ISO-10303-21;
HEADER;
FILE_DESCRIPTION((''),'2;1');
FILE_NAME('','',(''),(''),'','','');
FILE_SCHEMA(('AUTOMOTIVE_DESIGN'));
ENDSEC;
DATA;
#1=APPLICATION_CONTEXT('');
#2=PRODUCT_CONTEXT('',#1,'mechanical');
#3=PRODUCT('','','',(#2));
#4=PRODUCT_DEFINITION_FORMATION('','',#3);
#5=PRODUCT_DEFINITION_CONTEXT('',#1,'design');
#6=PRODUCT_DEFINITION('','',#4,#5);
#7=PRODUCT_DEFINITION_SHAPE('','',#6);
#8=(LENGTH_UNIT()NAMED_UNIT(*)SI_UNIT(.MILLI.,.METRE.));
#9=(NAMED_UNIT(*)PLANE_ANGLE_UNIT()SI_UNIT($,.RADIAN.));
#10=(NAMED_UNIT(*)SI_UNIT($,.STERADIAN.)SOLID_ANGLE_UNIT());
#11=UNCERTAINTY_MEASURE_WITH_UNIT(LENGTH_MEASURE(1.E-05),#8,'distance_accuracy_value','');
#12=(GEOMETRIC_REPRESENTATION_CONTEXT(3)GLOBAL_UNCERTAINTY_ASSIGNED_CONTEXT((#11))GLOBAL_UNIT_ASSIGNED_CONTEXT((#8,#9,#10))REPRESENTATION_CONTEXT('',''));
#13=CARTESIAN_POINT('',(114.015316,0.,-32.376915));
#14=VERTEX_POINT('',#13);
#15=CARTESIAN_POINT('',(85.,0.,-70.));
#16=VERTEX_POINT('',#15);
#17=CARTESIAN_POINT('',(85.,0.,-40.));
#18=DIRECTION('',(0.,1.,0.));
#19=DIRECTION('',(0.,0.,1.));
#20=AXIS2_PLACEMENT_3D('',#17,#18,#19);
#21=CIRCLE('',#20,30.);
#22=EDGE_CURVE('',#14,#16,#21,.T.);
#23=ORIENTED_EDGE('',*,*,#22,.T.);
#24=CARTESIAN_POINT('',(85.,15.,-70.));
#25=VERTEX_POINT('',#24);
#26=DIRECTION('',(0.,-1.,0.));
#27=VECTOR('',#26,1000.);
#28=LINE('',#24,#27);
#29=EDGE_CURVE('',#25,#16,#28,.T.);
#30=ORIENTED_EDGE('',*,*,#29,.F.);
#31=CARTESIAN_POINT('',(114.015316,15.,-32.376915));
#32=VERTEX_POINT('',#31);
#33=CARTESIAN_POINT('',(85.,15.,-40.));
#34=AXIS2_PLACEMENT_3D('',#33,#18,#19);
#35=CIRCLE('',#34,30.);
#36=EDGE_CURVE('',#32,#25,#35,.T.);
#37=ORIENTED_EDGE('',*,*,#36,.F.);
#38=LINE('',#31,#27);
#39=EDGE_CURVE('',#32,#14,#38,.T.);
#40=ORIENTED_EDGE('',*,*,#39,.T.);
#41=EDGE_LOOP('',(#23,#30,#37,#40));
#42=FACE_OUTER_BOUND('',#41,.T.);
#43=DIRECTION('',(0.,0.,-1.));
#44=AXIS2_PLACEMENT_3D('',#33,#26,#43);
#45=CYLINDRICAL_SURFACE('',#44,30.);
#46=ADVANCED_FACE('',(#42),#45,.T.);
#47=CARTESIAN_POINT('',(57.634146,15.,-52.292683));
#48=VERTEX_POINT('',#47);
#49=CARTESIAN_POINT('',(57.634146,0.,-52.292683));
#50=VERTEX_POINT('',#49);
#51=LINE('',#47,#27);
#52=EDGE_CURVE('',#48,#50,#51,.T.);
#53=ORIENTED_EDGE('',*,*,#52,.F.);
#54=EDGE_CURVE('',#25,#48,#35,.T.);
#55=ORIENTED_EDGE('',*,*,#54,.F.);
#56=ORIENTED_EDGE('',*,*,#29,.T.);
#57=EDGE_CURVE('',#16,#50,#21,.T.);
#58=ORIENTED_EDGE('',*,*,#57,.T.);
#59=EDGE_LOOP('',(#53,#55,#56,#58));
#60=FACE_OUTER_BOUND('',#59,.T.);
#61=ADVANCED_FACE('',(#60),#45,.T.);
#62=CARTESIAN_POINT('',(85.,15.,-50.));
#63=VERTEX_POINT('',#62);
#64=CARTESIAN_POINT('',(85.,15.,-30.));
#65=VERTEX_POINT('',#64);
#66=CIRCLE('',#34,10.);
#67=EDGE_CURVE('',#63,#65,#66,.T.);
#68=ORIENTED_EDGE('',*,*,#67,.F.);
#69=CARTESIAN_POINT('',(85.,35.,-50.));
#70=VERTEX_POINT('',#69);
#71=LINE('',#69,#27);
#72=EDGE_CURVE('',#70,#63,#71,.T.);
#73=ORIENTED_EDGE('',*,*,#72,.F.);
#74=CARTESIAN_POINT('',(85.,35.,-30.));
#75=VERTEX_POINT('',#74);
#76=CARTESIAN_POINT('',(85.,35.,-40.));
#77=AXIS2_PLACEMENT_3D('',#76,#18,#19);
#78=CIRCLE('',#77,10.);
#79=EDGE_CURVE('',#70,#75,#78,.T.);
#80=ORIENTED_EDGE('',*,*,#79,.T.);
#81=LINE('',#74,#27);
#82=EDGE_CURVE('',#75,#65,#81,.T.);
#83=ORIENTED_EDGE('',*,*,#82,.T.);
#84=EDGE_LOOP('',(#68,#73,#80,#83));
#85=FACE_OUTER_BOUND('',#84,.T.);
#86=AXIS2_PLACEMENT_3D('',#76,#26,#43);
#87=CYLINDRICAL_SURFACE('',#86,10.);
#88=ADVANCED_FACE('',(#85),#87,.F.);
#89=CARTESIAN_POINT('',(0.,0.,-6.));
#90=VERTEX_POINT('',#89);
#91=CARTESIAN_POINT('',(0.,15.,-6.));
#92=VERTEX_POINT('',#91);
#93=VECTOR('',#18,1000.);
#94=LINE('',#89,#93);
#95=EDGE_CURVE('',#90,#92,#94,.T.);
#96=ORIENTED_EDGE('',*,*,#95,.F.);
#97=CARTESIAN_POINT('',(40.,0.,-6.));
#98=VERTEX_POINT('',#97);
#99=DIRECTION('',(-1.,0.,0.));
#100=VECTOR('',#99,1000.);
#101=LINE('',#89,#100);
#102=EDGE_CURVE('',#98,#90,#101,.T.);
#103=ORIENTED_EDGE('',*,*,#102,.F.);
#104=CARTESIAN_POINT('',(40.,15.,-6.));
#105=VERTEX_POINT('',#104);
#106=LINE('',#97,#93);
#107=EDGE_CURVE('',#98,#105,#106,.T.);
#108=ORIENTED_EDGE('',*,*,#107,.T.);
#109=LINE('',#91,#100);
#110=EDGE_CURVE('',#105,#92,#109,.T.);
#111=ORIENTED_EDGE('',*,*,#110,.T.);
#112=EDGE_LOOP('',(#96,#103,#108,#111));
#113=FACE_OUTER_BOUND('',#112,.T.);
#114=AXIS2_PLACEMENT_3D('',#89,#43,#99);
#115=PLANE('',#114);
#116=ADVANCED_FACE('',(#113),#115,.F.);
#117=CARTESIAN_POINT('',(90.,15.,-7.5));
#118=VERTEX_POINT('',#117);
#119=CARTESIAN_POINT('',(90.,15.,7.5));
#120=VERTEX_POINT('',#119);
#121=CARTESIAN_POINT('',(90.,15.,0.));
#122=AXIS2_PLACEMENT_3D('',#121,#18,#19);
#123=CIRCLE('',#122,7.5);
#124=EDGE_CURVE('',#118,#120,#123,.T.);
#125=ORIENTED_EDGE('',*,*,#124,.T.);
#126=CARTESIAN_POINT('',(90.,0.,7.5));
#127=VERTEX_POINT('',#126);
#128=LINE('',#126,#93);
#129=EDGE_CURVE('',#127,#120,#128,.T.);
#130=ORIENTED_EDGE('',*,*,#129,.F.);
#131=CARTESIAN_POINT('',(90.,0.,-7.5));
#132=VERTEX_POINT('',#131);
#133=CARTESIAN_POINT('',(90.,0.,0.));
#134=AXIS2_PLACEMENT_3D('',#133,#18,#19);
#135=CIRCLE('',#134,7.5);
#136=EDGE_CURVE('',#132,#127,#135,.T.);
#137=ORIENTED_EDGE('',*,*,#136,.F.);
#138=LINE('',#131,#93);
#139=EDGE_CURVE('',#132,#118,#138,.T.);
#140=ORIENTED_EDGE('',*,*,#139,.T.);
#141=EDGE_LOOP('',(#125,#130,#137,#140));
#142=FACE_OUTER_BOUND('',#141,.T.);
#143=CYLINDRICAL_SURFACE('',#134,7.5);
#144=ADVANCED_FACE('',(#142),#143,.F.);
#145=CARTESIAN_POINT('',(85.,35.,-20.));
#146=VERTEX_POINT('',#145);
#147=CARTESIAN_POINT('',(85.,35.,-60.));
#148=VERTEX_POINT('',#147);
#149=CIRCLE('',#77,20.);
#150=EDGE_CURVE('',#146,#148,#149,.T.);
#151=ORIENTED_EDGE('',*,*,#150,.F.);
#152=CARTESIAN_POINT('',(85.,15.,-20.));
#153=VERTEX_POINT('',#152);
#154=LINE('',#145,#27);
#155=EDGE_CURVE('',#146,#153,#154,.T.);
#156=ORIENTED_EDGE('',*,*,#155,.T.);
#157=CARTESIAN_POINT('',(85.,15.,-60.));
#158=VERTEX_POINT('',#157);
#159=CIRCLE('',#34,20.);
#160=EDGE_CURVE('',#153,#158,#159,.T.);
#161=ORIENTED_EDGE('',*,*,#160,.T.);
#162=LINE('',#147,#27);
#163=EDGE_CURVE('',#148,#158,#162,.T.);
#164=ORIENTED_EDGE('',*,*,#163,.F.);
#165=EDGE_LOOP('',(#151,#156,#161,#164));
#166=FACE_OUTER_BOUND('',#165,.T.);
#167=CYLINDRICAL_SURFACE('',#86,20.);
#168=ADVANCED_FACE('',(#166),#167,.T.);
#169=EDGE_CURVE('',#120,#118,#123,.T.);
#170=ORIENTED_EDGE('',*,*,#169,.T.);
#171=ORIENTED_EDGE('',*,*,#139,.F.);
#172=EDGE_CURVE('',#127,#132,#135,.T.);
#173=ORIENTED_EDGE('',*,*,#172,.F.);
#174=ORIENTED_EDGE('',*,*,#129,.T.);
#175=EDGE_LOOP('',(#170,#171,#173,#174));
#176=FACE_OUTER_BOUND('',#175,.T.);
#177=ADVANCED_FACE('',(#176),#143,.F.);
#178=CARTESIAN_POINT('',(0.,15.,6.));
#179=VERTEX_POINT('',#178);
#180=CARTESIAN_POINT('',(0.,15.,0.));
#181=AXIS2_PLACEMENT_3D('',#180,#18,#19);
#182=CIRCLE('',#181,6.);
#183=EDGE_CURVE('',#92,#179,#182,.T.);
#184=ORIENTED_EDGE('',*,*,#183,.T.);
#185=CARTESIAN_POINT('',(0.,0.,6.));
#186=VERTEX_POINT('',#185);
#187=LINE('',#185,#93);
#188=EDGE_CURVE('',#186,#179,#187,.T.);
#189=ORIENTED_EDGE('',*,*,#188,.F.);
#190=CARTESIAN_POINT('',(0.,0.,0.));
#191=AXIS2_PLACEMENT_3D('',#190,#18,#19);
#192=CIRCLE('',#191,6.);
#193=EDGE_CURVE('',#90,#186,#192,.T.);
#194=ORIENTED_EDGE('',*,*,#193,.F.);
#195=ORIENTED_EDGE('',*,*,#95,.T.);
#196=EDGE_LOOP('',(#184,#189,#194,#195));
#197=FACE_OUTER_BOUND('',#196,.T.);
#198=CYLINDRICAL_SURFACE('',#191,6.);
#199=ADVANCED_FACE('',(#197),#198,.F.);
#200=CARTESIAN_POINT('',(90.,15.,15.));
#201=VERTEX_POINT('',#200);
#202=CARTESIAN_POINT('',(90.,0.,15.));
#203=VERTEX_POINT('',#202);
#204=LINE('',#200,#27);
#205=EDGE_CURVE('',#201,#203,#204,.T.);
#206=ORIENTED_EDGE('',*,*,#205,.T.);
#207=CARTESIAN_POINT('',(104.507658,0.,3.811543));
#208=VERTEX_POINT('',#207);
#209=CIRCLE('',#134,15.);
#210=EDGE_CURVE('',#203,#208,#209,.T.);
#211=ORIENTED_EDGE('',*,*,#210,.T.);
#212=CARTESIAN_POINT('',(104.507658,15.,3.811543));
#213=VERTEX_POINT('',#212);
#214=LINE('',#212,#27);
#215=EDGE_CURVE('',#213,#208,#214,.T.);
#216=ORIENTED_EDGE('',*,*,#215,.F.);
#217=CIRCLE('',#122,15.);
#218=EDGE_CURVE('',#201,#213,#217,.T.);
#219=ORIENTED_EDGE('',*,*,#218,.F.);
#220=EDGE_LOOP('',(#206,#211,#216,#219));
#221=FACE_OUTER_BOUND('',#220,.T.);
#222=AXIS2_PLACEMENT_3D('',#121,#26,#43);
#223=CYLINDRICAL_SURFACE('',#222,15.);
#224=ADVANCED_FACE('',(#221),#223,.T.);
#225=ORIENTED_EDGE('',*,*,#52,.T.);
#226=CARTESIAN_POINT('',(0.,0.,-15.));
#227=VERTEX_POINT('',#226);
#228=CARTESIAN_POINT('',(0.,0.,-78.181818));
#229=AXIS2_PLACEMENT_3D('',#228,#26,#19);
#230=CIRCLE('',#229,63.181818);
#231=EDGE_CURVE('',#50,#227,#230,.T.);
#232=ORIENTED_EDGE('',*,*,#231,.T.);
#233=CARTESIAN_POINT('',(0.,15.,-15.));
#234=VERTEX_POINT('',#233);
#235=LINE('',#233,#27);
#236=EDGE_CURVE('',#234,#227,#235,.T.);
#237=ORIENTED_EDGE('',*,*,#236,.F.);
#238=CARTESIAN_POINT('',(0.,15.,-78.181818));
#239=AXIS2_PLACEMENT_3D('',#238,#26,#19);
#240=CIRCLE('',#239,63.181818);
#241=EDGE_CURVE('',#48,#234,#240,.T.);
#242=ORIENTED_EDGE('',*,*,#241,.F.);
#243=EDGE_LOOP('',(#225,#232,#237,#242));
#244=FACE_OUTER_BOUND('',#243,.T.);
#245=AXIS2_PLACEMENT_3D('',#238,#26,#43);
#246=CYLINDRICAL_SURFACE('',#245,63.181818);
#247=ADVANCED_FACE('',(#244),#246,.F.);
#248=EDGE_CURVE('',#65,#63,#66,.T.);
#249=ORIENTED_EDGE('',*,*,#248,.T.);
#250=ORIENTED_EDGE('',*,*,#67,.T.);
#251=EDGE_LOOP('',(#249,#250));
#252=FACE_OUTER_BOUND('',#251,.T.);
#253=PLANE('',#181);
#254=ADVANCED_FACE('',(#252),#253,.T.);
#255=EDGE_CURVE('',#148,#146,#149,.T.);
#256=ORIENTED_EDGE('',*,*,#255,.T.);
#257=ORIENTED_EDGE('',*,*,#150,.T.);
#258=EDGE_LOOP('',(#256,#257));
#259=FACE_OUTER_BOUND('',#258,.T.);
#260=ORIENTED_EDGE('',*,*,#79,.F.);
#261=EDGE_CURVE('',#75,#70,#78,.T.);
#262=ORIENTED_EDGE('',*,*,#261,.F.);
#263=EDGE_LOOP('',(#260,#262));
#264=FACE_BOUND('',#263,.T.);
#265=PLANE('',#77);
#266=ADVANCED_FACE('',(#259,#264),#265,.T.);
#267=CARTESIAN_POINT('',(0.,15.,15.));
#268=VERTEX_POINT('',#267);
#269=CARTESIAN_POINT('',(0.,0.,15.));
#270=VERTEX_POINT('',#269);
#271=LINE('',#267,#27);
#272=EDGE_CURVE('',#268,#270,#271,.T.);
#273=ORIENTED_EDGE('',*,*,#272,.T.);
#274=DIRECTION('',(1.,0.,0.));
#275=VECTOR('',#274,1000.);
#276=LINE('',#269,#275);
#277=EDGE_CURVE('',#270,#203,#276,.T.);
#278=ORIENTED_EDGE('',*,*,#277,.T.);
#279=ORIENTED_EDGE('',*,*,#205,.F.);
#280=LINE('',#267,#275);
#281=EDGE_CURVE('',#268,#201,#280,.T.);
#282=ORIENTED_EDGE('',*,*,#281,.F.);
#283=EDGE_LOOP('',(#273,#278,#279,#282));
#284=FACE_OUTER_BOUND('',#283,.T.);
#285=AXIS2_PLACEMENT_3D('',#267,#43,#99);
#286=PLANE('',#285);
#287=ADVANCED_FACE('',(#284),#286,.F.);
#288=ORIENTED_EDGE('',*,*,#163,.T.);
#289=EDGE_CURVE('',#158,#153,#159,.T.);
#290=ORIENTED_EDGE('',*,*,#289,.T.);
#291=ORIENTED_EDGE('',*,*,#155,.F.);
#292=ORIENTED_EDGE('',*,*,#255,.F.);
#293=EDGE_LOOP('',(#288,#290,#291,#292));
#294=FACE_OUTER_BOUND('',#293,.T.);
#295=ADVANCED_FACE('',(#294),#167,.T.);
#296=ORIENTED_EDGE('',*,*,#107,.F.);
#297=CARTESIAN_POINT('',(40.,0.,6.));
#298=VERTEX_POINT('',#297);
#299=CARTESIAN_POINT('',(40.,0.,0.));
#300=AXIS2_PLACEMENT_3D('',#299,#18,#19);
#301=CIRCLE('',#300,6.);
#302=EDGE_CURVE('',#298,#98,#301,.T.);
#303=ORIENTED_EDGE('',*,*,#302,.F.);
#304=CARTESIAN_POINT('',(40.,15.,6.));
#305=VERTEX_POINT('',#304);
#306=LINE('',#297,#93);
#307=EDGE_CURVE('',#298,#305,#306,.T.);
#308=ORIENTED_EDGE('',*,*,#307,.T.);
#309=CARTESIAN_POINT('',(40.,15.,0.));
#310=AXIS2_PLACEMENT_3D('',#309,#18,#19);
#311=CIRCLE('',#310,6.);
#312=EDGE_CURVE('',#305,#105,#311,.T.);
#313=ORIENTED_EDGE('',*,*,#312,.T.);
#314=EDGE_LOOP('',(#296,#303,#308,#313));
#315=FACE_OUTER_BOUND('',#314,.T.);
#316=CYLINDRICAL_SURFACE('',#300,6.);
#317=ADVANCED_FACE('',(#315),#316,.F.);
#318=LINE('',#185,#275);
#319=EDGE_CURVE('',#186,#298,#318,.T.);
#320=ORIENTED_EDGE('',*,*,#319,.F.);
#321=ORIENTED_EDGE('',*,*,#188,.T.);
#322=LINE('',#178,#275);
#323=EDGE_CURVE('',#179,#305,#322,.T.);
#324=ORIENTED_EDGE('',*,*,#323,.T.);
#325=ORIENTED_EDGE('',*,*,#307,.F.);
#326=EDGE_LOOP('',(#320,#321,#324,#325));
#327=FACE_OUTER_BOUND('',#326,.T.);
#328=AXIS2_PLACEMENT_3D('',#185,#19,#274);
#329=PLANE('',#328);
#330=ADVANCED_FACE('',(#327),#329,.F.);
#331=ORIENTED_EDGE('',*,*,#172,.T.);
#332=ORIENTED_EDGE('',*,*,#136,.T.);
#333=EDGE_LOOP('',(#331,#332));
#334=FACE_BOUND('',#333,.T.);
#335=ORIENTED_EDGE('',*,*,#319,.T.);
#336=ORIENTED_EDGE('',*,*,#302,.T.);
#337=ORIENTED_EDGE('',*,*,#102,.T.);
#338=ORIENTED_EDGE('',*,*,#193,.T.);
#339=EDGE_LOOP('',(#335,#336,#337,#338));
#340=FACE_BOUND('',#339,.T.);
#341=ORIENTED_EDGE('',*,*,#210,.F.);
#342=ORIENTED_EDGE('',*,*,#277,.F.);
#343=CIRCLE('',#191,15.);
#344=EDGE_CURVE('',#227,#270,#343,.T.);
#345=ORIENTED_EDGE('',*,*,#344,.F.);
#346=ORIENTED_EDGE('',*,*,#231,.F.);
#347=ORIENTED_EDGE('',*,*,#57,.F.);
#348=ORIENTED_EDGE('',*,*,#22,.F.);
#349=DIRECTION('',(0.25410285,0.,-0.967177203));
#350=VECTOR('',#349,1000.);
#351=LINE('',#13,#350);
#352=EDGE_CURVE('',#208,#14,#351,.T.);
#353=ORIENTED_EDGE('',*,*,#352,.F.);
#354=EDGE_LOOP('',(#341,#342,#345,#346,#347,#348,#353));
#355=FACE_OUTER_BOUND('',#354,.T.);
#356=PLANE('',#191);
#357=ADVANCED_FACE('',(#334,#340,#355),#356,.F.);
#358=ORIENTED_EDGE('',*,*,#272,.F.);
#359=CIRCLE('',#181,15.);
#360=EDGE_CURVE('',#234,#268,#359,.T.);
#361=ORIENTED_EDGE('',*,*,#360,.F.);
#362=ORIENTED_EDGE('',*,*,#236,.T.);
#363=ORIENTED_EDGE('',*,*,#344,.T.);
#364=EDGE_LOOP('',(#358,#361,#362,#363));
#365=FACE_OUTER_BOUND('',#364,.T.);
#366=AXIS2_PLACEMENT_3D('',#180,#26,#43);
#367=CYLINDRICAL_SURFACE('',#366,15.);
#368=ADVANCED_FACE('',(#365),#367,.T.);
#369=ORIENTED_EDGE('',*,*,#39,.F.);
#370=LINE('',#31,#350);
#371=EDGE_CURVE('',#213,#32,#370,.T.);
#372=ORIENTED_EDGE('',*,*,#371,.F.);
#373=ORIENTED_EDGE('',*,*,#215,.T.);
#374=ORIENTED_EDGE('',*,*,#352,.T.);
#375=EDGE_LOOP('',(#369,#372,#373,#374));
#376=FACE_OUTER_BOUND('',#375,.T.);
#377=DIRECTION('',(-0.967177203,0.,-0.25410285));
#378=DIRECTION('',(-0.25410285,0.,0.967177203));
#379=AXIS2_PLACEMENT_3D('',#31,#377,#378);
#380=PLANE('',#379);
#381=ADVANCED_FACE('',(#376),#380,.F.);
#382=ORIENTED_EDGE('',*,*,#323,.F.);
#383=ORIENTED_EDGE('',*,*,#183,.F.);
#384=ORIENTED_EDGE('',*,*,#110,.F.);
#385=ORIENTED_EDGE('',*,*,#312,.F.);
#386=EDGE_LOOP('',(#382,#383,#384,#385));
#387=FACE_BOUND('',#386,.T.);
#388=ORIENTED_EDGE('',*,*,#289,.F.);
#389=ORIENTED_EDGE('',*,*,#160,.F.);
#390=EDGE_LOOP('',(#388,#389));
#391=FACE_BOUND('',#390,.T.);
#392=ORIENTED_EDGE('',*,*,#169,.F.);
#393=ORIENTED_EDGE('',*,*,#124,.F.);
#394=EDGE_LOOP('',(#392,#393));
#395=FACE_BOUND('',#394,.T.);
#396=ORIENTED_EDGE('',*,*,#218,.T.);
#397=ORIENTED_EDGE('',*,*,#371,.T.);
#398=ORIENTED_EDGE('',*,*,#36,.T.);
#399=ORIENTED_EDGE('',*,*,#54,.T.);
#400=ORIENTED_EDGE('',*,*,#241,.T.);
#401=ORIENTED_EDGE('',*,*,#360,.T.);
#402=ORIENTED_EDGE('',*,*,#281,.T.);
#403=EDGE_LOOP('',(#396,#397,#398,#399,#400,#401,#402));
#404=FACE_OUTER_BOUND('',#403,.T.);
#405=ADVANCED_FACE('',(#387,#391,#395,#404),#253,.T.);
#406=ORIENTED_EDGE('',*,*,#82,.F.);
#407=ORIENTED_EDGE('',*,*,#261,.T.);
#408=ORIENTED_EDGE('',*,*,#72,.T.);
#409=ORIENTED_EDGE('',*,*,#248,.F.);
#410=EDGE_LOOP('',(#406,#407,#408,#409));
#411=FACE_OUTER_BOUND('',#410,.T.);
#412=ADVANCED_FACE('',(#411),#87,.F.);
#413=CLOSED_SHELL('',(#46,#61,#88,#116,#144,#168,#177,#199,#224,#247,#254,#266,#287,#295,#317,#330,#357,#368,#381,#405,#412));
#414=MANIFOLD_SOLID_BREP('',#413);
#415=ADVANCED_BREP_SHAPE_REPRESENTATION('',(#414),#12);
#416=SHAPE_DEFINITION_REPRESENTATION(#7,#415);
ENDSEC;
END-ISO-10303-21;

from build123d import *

# Parameters (mm, degrees)
LINK_PLATE_15MM_DEPTH        = 15
SLOT_CUT_DEPTH               = 136.462171841
THROUGH_HOLE_PROFILE_R       = 7.5
THROUGH_HOLE_CUT_DEPTH       = 15
PIVOT_BOSS_PROFILE_40_20_R   = 20
PIVOT_BOSS_PROFILE_40_20_R_2 = 10
PIVOT_BOSS_40_DEPTH          = 20


with BuildPart() as part:
    # Link Plate Profile → Link Plate 15mm (new body)
    with BuildSketch(Plane(origin=(0, 0, 0), x_dir=(1, 0, 0), z_dir=(0, 1, 0))):
        with BuildLine():
            Line((114.015316087, 32.376914511), (104.507658043, -3.811542745))
            ThreePointArc((104.507658043, -3.811542745), (99.16042736, -11.877986807), (90, -15))
            Line((90, -15), (0, -15))
            ThreePointArc((0, -15), (-15, 0), (0, 15))
            ThreePointArc((0, 15), (34.323603484, 25.136249162), (57.634146341, 52.292682927))
            ThreePointArc((57.634146341, 52.292682927), (94.991978757, 68.287105906), (114.015316087, 32.376914511))
        make_face()
    extrude(amount=LINK_PLATE_15MM_DEPTH)

    # Slot Profile → Slot Cut (cut, through all)
    with BuildSketch(Plane(origin=(0, 15, 0), x_dir=(1, 0, 0), z_dir=(0, 1, 0))):
        with BuildLine():
            Line((0, 6), (40, 6))
            ThreePointArc((40, 6), (46, 0), (40, -6))
            Line((40, -6), (0, -6))
            ThreePointArc((0, -6), (-6, 0), (0, 6))
        make_face()
    extrude(amount=-SLOT_CUT_DEPTH, mode=Mode.SUBTRACT)

    # Through Hole Profile → Through Hole Cut (cut)
    with BuildSketch(Plane(origin=(0, 15, 0), x_dir=(1, 0, 0), z_dir=(0, 1, 0))):
        with Locations(Location((90, 0, 0), (0, 0, 270))):
            Circle(THROUGH_HOLE_PROFILE_R)
    extrude(amount=-THROUGH_HOLE_CUT_DEPTH, mode=Mode.SUBTRACT)

    # Pivot Boss Profile Ø40-Ø20 → Pivot Boss Ø40 (add)
    with BuildSketch(Plane(origin=(0, 15, 0), x_dir=(1, 0, 0), z_dir=(0, 1, 0))):
        with Locations(Location((85, 40, 0), (0, 0, 270))):
            Circle(PIVOT_BOSS_PROFILE_40_20_R)
        with Locations(Location((85, 40, 0), (0, 0, 270))):
            Circle(PIVOT_BOSS_PROFILE_40_20_R_2, mode=Mode.SUBTRACT)
    extrude(amount=PIVOT_BOSS_40_DEPTH)


solid = part.part
